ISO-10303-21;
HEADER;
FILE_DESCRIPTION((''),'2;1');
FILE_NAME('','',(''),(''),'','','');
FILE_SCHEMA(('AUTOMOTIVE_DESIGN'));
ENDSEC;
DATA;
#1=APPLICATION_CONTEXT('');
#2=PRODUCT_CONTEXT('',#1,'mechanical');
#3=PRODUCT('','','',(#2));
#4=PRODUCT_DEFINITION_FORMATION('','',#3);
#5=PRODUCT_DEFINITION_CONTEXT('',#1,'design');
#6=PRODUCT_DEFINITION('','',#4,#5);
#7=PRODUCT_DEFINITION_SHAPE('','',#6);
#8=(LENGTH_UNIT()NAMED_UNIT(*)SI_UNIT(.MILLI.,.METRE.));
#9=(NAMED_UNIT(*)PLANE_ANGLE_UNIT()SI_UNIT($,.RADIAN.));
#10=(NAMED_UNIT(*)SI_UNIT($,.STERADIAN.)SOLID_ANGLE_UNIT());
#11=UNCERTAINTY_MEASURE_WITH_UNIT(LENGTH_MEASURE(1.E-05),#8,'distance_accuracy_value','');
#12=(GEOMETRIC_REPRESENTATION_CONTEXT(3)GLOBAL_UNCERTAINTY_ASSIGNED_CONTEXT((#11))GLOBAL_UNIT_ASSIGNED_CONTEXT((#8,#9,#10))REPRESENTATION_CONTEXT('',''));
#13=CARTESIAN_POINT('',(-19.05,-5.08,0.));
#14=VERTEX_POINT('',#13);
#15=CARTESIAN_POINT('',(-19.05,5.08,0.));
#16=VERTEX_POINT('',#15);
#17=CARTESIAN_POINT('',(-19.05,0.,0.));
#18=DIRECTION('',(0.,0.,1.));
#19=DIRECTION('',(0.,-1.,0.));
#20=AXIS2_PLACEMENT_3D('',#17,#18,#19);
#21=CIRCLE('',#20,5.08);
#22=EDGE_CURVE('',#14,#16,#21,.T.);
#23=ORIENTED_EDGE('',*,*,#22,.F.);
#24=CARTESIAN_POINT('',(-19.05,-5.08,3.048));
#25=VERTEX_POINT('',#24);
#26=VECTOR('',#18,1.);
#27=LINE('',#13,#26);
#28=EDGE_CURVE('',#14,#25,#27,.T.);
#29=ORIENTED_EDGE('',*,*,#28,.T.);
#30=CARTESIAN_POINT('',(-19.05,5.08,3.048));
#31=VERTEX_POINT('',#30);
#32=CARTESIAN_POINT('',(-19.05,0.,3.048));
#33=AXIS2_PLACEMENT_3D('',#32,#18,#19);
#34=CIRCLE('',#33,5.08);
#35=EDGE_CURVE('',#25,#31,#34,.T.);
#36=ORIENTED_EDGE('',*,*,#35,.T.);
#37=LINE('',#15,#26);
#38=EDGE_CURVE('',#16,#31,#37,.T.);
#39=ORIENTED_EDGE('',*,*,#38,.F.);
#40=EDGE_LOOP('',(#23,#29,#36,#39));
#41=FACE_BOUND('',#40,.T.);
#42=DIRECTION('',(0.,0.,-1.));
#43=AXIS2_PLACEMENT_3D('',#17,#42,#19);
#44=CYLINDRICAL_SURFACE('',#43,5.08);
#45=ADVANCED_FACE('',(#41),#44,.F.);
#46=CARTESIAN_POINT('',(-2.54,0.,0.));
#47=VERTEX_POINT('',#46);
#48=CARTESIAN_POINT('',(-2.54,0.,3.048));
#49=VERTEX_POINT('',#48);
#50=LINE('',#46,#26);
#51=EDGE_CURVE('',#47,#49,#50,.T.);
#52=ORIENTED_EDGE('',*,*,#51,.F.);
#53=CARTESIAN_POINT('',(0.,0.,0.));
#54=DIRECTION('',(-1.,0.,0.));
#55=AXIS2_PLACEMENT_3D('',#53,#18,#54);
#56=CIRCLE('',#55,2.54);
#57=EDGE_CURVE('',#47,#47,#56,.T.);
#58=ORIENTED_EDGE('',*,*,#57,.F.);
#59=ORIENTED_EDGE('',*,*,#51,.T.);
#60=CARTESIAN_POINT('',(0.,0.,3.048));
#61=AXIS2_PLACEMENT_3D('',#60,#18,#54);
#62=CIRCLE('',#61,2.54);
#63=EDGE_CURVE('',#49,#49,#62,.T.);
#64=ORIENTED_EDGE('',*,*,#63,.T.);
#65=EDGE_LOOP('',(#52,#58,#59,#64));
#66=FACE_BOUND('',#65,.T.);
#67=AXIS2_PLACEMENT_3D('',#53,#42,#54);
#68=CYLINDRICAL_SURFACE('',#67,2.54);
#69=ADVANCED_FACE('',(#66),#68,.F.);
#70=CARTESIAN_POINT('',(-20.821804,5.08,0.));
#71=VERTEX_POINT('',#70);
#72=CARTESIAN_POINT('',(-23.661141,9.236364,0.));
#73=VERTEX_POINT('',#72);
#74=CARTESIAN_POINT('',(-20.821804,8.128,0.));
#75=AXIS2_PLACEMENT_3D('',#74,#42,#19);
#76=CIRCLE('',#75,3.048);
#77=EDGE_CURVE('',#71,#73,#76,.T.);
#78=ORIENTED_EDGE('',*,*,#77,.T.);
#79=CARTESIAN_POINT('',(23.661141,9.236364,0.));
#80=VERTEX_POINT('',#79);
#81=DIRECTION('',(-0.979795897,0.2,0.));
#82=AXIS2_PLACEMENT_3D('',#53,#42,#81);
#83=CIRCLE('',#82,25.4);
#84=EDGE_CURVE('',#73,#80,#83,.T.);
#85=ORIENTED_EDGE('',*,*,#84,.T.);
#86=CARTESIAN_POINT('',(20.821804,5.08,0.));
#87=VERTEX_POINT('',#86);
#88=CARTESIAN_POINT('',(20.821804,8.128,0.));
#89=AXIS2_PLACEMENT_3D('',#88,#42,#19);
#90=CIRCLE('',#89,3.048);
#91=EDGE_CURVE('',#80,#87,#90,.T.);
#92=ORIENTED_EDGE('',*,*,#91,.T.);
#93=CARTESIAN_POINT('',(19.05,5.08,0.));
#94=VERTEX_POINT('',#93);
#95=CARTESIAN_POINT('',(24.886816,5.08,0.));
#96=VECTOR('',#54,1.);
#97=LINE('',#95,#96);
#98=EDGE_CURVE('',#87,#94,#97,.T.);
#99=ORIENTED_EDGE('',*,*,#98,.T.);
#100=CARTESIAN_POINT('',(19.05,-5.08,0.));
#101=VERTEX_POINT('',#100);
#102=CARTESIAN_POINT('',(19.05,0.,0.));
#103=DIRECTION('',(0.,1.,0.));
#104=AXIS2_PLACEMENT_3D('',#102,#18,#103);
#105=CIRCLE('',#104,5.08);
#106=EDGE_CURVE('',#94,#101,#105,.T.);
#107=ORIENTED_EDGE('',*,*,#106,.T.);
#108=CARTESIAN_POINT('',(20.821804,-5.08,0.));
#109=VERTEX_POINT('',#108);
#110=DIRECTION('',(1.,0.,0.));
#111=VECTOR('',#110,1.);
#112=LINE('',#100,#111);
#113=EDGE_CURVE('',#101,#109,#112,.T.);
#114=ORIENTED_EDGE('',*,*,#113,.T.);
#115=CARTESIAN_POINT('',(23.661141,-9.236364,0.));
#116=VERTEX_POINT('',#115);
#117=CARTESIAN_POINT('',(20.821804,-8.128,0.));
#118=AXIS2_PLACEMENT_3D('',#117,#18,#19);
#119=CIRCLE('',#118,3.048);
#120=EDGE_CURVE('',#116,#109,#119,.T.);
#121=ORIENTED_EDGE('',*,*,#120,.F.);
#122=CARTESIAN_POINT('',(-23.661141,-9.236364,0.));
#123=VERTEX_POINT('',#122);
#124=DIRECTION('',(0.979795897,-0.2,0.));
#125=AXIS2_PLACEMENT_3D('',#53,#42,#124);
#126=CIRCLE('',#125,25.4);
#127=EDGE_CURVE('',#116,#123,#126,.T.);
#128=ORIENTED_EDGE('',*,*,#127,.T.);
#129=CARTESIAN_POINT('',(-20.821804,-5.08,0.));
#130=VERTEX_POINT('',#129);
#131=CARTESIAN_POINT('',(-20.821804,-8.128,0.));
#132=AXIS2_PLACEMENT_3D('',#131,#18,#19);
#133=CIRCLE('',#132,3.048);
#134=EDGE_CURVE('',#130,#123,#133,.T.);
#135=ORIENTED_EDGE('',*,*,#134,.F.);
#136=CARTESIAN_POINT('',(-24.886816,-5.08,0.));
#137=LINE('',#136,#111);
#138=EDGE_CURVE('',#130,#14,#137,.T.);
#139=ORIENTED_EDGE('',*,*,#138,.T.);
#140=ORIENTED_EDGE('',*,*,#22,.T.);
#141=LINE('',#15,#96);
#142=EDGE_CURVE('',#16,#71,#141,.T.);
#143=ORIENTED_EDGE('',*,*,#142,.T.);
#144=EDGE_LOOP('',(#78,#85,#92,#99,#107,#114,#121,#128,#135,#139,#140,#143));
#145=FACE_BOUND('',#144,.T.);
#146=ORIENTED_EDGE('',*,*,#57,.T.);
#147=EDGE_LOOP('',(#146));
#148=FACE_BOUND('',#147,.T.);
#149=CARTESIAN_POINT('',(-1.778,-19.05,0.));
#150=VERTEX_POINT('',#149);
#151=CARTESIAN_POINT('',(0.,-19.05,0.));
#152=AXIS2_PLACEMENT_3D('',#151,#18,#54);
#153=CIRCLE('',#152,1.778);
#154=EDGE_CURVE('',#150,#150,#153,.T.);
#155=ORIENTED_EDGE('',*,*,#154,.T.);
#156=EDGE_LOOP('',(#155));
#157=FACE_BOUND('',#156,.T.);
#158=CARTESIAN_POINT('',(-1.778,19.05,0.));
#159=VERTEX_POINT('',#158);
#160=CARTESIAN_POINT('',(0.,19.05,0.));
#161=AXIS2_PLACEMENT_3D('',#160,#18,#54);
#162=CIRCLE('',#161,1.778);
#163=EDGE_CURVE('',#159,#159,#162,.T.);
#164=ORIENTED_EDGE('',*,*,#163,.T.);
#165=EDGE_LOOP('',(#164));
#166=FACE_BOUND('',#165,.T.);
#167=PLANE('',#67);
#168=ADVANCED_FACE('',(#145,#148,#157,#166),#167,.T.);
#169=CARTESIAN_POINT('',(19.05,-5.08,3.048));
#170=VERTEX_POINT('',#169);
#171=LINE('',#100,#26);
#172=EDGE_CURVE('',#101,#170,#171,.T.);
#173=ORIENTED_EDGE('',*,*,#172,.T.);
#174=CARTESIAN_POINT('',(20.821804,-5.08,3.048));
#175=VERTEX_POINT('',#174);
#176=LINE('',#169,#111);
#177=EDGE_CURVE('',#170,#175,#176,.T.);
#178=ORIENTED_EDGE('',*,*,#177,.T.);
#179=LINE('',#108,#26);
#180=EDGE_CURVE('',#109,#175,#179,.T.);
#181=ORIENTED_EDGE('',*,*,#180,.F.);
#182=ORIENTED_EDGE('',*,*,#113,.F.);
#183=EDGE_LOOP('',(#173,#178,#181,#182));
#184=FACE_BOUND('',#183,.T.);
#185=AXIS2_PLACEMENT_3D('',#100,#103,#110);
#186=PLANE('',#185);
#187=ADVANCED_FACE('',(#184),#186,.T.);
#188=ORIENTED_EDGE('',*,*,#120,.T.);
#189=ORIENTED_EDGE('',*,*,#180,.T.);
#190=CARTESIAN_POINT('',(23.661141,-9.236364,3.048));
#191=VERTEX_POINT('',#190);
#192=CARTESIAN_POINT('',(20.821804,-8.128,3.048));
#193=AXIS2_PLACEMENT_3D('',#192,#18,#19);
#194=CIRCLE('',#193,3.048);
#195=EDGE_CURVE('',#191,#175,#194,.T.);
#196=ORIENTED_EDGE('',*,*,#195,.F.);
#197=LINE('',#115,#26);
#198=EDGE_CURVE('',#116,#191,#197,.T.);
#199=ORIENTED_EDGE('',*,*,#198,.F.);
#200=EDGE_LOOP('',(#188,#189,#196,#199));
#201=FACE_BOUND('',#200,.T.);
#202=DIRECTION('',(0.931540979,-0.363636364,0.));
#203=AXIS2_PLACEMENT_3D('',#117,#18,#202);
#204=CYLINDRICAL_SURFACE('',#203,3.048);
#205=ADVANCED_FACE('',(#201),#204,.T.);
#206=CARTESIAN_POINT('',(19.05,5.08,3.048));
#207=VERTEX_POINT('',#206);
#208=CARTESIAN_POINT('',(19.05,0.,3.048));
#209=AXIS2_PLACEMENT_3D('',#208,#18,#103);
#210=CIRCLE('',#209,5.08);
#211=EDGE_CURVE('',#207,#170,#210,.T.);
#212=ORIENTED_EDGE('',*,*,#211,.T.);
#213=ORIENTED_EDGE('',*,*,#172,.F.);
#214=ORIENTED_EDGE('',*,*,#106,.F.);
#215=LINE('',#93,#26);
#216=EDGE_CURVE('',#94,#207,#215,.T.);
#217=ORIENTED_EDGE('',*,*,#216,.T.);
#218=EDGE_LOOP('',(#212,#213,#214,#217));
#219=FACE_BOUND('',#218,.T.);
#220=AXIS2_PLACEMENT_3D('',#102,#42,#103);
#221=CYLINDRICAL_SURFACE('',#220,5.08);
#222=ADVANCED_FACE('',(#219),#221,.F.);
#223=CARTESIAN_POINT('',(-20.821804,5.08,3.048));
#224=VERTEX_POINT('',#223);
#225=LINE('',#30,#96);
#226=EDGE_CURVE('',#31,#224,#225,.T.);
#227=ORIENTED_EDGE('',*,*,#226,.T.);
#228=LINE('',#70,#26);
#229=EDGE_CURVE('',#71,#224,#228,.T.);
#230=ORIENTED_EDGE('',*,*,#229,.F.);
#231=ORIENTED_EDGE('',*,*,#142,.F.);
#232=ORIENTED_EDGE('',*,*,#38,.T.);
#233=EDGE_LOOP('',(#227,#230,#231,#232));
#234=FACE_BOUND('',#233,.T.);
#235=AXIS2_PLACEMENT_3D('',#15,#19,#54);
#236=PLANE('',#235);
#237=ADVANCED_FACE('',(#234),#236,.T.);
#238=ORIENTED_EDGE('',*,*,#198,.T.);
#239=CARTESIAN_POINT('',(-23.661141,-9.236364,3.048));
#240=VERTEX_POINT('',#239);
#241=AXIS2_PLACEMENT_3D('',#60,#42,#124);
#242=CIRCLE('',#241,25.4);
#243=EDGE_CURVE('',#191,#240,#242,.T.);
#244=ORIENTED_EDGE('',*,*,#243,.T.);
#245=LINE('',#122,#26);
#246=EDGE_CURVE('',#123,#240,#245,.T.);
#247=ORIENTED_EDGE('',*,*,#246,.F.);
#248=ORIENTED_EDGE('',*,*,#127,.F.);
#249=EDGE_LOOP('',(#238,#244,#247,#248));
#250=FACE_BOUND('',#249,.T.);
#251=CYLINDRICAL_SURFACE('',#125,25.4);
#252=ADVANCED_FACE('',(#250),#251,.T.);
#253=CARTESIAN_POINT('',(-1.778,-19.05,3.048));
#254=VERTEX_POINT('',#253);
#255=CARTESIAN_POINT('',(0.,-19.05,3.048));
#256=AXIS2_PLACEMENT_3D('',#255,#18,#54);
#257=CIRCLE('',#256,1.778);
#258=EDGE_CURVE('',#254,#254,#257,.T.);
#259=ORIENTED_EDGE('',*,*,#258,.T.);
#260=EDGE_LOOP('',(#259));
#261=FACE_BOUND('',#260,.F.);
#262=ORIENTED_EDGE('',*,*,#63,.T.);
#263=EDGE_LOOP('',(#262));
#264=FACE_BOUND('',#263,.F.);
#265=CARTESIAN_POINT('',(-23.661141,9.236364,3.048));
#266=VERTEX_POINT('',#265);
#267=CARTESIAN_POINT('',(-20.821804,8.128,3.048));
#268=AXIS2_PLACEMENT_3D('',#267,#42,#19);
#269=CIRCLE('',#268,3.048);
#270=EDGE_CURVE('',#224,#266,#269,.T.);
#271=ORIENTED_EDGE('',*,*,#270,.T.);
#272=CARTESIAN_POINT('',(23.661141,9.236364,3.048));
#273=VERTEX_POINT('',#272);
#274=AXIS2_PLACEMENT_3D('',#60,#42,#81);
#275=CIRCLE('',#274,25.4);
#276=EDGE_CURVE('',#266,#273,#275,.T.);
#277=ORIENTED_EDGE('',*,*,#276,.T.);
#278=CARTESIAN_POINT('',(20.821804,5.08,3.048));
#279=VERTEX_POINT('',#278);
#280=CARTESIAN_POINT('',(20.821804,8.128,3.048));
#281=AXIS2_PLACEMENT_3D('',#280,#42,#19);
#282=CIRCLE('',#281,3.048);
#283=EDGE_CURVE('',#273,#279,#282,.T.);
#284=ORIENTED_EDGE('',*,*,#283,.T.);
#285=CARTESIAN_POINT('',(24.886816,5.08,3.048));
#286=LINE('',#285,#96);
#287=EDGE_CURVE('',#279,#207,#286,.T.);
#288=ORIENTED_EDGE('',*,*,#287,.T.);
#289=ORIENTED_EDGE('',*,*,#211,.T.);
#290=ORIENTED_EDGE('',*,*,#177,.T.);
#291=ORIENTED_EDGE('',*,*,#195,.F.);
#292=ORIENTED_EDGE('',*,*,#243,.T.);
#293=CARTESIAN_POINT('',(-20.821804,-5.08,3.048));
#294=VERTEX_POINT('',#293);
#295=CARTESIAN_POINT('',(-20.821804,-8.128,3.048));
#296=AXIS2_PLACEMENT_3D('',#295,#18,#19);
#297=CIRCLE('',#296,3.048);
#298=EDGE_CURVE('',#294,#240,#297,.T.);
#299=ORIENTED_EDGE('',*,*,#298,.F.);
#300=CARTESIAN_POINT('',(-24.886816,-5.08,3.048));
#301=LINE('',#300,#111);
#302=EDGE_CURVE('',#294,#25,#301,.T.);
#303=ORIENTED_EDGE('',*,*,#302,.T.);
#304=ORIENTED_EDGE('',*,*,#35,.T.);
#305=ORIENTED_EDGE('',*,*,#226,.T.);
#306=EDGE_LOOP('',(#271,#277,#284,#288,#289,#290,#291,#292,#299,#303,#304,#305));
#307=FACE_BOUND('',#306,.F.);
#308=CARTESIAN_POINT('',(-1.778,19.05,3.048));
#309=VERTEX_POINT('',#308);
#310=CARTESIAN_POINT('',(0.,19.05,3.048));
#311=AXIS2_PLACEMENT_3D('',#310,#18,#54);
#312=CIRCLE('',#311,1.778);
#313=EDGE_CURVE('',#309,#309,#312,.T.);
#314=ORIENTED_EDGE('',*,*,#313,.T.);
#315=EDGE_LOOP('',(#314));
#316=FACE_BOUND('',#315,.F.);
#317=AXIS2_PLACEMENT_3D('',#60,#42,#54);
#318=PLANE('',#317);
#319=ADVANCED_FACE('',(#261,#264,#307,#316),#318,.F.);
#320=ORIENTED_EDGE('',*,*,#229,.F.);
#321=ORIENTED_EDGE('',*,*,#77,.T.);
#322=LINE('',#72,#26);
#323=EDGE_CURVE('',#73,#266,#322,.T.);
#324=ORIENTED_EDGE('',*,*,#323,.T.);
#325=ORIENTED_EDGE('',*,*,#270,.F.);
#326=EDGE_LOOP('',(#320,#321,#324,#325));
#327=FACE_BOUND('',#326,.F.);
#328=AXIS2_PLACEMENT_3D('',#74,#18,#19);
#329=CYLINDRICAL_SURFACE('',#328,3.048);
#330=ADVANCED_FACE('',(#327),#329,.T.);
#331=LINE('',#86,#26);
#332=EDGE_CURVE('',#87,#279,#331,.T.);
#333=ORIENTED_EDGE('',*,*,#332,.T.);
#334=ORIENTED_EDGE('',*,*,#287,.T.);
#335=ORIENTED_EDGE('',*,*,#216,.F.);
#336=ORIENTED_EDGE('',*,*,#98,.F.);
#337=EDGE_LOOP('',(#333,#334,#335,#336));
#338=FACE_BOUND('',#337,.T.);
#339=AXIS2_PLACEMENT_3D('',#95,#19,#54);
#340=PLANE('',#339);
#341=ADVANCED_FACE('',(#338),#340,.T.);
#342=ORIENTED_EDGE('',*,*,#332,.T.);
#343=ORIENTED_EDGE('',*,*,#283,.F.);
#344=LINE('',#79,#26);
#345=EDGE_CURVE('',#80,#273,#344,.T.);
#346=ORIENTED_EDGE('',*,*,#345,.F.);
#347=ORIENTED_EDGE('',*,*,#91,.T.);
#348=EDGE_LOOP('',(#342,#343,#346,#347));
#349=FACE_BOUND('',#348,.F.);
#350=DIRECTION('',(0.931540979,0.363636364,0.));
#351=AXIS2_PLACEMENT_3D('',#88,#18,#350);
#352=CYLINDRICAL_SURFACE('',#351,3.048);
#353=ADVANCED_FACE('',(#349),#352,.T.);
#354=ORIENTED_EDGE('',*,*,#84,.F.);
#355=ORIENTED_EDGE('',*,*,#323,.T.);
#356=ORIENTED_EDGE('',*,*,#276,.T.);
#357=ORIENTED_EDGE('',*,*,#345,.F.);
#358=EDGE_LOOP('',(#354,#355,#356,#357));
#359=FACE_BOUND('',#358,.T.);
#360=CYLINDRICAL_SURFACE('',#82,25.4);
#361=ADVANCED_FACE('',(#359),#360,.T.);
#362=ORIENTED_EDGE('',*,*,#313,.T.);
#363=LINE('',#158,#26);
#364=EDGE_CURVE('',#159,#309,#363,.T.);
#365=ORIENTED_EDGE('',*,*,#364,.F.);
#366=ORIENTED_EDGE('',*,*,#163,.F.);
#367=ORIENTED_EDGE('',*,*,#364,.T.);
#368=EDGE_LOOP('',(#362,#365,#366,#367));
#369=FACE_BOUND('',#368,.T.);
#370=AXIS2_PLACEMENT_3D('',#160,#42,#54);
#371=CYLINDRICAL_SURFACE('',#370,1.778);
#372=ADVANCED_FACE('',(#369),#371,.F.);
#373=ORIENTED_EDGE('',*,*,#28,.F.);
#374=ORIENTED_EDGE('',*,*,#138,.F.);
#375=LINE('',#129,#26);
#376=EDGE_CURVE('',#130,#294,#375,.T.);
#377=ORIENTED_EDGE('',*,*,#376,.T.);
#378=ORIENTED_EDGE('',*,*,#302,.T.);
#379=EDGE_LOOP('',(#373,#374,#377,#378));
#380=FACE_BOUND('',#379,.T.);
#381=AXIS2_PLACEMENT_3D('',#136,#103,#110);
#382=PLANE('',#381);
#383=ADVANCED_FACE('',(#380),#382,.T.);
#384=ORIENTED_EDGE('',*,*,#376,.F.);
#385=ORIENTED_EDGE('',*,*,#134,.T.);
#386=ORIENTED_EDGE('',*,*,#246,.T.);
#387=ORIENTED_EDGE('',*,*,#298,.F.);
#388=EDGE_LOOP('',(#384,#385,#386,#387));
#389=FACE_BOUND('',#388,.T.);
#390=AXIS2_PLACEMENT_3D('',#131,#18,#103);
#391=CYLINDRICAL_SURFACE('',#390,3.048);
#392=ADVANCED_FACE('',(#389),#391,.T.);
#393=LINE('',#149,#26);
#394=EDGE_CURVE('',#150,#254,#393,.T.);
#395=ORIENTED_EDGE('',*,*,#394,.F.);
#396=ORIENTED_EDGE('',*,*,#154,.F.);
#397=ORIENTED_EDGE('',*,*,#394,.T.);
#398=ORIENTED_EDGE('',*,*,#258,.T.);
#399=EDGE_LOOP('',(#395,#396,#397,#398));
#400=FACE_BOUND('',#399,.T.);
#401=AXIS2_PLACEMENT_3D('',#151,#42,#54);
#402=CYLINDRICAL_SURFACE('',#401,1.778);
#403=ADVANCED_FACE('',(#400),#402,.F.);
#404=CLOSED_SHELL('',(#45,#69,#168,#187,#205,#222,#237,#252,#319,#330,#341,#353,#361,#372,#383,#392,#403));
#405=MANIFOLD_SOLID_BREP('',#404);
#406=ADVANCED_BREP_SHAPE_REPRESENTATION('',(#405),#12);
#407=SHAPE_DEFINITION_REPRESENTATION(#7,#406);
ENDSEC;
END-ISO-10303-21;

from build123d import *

# Parameters (mm, degrees)
PLATE_PROFILE_SKETCH_R   = 1.778
PLATE_PROFILE_SKETCH_R_2 = 2.54
PLATE_BODY_0_12IN_DEPTH  = 3.048
FILLETS_R0_12IN_R        = 3.048


with BuildPart() as part:
    # Plate Profile Sketch → Plate Body 0.12in (new body)
    with BuildSketch(Plane.XY):
        with BuildLine():
            Line((-19.05, 5.08), (-24.886815787, 5.08))
            ThreePointArc((-24.886815787, 5.08), (0, 25.4), (24.886815787, 5.08))
            Line((24.886815787, 5.08), (19.05, 5.08))
            ThreePointArc((19.05, 5.08), (13.97, 0), (19.05, -5.08))
            Line((19.05, -5.08), (24.886815787, -5.08))
            ThreePointArc((24.886815787, -5.08), (0, -25.4), (-24.886815787, -5.08))
            Line((-24.886815787, -5.08), (-19.05, -5.08))
            ThreePointArc((-19.05, -5.08), (-13.97, 0), (-19.05, 5.08))
        make_face()
        with Locations(Location((0, 19.05, 0), (0, 0, 180))):
            Circle(PLATE_PROFILE_SKETCH_R, mode=Mode.SUBTRACT)
        with Locations(Location((0, -19.05, 0), (0, 0, 180))):
            Circle(PLATE_PROFILE_SKETCH_R, mode=Mode.SUBTRACT)
        with Locations(Location((0, 0, 0), (0, 0, 180))):
            Circle(PLATE_PROFILE_SKETCH_R_2, mode=Mode.SUBTRACT)
    extrude(amount=PLATE_BODY_0_12IN_DEPTH)

    # Fillets R0.12in
    fillets_r0_12in_edges = [part.edges().sort_by_distance(p)[0] for p in [
        (-24.886815787, 5.08, 1.524),
        (24.886815787, 5.08, 1.524),
        (24.886815787, -5.08, 1.524),
        (-24.886815787, -5.08, 1.524),
    ]]
    fillet(fillets_r0_12in_edges, radius=FILLETS_R0_12IN_R)


solid = part.part
